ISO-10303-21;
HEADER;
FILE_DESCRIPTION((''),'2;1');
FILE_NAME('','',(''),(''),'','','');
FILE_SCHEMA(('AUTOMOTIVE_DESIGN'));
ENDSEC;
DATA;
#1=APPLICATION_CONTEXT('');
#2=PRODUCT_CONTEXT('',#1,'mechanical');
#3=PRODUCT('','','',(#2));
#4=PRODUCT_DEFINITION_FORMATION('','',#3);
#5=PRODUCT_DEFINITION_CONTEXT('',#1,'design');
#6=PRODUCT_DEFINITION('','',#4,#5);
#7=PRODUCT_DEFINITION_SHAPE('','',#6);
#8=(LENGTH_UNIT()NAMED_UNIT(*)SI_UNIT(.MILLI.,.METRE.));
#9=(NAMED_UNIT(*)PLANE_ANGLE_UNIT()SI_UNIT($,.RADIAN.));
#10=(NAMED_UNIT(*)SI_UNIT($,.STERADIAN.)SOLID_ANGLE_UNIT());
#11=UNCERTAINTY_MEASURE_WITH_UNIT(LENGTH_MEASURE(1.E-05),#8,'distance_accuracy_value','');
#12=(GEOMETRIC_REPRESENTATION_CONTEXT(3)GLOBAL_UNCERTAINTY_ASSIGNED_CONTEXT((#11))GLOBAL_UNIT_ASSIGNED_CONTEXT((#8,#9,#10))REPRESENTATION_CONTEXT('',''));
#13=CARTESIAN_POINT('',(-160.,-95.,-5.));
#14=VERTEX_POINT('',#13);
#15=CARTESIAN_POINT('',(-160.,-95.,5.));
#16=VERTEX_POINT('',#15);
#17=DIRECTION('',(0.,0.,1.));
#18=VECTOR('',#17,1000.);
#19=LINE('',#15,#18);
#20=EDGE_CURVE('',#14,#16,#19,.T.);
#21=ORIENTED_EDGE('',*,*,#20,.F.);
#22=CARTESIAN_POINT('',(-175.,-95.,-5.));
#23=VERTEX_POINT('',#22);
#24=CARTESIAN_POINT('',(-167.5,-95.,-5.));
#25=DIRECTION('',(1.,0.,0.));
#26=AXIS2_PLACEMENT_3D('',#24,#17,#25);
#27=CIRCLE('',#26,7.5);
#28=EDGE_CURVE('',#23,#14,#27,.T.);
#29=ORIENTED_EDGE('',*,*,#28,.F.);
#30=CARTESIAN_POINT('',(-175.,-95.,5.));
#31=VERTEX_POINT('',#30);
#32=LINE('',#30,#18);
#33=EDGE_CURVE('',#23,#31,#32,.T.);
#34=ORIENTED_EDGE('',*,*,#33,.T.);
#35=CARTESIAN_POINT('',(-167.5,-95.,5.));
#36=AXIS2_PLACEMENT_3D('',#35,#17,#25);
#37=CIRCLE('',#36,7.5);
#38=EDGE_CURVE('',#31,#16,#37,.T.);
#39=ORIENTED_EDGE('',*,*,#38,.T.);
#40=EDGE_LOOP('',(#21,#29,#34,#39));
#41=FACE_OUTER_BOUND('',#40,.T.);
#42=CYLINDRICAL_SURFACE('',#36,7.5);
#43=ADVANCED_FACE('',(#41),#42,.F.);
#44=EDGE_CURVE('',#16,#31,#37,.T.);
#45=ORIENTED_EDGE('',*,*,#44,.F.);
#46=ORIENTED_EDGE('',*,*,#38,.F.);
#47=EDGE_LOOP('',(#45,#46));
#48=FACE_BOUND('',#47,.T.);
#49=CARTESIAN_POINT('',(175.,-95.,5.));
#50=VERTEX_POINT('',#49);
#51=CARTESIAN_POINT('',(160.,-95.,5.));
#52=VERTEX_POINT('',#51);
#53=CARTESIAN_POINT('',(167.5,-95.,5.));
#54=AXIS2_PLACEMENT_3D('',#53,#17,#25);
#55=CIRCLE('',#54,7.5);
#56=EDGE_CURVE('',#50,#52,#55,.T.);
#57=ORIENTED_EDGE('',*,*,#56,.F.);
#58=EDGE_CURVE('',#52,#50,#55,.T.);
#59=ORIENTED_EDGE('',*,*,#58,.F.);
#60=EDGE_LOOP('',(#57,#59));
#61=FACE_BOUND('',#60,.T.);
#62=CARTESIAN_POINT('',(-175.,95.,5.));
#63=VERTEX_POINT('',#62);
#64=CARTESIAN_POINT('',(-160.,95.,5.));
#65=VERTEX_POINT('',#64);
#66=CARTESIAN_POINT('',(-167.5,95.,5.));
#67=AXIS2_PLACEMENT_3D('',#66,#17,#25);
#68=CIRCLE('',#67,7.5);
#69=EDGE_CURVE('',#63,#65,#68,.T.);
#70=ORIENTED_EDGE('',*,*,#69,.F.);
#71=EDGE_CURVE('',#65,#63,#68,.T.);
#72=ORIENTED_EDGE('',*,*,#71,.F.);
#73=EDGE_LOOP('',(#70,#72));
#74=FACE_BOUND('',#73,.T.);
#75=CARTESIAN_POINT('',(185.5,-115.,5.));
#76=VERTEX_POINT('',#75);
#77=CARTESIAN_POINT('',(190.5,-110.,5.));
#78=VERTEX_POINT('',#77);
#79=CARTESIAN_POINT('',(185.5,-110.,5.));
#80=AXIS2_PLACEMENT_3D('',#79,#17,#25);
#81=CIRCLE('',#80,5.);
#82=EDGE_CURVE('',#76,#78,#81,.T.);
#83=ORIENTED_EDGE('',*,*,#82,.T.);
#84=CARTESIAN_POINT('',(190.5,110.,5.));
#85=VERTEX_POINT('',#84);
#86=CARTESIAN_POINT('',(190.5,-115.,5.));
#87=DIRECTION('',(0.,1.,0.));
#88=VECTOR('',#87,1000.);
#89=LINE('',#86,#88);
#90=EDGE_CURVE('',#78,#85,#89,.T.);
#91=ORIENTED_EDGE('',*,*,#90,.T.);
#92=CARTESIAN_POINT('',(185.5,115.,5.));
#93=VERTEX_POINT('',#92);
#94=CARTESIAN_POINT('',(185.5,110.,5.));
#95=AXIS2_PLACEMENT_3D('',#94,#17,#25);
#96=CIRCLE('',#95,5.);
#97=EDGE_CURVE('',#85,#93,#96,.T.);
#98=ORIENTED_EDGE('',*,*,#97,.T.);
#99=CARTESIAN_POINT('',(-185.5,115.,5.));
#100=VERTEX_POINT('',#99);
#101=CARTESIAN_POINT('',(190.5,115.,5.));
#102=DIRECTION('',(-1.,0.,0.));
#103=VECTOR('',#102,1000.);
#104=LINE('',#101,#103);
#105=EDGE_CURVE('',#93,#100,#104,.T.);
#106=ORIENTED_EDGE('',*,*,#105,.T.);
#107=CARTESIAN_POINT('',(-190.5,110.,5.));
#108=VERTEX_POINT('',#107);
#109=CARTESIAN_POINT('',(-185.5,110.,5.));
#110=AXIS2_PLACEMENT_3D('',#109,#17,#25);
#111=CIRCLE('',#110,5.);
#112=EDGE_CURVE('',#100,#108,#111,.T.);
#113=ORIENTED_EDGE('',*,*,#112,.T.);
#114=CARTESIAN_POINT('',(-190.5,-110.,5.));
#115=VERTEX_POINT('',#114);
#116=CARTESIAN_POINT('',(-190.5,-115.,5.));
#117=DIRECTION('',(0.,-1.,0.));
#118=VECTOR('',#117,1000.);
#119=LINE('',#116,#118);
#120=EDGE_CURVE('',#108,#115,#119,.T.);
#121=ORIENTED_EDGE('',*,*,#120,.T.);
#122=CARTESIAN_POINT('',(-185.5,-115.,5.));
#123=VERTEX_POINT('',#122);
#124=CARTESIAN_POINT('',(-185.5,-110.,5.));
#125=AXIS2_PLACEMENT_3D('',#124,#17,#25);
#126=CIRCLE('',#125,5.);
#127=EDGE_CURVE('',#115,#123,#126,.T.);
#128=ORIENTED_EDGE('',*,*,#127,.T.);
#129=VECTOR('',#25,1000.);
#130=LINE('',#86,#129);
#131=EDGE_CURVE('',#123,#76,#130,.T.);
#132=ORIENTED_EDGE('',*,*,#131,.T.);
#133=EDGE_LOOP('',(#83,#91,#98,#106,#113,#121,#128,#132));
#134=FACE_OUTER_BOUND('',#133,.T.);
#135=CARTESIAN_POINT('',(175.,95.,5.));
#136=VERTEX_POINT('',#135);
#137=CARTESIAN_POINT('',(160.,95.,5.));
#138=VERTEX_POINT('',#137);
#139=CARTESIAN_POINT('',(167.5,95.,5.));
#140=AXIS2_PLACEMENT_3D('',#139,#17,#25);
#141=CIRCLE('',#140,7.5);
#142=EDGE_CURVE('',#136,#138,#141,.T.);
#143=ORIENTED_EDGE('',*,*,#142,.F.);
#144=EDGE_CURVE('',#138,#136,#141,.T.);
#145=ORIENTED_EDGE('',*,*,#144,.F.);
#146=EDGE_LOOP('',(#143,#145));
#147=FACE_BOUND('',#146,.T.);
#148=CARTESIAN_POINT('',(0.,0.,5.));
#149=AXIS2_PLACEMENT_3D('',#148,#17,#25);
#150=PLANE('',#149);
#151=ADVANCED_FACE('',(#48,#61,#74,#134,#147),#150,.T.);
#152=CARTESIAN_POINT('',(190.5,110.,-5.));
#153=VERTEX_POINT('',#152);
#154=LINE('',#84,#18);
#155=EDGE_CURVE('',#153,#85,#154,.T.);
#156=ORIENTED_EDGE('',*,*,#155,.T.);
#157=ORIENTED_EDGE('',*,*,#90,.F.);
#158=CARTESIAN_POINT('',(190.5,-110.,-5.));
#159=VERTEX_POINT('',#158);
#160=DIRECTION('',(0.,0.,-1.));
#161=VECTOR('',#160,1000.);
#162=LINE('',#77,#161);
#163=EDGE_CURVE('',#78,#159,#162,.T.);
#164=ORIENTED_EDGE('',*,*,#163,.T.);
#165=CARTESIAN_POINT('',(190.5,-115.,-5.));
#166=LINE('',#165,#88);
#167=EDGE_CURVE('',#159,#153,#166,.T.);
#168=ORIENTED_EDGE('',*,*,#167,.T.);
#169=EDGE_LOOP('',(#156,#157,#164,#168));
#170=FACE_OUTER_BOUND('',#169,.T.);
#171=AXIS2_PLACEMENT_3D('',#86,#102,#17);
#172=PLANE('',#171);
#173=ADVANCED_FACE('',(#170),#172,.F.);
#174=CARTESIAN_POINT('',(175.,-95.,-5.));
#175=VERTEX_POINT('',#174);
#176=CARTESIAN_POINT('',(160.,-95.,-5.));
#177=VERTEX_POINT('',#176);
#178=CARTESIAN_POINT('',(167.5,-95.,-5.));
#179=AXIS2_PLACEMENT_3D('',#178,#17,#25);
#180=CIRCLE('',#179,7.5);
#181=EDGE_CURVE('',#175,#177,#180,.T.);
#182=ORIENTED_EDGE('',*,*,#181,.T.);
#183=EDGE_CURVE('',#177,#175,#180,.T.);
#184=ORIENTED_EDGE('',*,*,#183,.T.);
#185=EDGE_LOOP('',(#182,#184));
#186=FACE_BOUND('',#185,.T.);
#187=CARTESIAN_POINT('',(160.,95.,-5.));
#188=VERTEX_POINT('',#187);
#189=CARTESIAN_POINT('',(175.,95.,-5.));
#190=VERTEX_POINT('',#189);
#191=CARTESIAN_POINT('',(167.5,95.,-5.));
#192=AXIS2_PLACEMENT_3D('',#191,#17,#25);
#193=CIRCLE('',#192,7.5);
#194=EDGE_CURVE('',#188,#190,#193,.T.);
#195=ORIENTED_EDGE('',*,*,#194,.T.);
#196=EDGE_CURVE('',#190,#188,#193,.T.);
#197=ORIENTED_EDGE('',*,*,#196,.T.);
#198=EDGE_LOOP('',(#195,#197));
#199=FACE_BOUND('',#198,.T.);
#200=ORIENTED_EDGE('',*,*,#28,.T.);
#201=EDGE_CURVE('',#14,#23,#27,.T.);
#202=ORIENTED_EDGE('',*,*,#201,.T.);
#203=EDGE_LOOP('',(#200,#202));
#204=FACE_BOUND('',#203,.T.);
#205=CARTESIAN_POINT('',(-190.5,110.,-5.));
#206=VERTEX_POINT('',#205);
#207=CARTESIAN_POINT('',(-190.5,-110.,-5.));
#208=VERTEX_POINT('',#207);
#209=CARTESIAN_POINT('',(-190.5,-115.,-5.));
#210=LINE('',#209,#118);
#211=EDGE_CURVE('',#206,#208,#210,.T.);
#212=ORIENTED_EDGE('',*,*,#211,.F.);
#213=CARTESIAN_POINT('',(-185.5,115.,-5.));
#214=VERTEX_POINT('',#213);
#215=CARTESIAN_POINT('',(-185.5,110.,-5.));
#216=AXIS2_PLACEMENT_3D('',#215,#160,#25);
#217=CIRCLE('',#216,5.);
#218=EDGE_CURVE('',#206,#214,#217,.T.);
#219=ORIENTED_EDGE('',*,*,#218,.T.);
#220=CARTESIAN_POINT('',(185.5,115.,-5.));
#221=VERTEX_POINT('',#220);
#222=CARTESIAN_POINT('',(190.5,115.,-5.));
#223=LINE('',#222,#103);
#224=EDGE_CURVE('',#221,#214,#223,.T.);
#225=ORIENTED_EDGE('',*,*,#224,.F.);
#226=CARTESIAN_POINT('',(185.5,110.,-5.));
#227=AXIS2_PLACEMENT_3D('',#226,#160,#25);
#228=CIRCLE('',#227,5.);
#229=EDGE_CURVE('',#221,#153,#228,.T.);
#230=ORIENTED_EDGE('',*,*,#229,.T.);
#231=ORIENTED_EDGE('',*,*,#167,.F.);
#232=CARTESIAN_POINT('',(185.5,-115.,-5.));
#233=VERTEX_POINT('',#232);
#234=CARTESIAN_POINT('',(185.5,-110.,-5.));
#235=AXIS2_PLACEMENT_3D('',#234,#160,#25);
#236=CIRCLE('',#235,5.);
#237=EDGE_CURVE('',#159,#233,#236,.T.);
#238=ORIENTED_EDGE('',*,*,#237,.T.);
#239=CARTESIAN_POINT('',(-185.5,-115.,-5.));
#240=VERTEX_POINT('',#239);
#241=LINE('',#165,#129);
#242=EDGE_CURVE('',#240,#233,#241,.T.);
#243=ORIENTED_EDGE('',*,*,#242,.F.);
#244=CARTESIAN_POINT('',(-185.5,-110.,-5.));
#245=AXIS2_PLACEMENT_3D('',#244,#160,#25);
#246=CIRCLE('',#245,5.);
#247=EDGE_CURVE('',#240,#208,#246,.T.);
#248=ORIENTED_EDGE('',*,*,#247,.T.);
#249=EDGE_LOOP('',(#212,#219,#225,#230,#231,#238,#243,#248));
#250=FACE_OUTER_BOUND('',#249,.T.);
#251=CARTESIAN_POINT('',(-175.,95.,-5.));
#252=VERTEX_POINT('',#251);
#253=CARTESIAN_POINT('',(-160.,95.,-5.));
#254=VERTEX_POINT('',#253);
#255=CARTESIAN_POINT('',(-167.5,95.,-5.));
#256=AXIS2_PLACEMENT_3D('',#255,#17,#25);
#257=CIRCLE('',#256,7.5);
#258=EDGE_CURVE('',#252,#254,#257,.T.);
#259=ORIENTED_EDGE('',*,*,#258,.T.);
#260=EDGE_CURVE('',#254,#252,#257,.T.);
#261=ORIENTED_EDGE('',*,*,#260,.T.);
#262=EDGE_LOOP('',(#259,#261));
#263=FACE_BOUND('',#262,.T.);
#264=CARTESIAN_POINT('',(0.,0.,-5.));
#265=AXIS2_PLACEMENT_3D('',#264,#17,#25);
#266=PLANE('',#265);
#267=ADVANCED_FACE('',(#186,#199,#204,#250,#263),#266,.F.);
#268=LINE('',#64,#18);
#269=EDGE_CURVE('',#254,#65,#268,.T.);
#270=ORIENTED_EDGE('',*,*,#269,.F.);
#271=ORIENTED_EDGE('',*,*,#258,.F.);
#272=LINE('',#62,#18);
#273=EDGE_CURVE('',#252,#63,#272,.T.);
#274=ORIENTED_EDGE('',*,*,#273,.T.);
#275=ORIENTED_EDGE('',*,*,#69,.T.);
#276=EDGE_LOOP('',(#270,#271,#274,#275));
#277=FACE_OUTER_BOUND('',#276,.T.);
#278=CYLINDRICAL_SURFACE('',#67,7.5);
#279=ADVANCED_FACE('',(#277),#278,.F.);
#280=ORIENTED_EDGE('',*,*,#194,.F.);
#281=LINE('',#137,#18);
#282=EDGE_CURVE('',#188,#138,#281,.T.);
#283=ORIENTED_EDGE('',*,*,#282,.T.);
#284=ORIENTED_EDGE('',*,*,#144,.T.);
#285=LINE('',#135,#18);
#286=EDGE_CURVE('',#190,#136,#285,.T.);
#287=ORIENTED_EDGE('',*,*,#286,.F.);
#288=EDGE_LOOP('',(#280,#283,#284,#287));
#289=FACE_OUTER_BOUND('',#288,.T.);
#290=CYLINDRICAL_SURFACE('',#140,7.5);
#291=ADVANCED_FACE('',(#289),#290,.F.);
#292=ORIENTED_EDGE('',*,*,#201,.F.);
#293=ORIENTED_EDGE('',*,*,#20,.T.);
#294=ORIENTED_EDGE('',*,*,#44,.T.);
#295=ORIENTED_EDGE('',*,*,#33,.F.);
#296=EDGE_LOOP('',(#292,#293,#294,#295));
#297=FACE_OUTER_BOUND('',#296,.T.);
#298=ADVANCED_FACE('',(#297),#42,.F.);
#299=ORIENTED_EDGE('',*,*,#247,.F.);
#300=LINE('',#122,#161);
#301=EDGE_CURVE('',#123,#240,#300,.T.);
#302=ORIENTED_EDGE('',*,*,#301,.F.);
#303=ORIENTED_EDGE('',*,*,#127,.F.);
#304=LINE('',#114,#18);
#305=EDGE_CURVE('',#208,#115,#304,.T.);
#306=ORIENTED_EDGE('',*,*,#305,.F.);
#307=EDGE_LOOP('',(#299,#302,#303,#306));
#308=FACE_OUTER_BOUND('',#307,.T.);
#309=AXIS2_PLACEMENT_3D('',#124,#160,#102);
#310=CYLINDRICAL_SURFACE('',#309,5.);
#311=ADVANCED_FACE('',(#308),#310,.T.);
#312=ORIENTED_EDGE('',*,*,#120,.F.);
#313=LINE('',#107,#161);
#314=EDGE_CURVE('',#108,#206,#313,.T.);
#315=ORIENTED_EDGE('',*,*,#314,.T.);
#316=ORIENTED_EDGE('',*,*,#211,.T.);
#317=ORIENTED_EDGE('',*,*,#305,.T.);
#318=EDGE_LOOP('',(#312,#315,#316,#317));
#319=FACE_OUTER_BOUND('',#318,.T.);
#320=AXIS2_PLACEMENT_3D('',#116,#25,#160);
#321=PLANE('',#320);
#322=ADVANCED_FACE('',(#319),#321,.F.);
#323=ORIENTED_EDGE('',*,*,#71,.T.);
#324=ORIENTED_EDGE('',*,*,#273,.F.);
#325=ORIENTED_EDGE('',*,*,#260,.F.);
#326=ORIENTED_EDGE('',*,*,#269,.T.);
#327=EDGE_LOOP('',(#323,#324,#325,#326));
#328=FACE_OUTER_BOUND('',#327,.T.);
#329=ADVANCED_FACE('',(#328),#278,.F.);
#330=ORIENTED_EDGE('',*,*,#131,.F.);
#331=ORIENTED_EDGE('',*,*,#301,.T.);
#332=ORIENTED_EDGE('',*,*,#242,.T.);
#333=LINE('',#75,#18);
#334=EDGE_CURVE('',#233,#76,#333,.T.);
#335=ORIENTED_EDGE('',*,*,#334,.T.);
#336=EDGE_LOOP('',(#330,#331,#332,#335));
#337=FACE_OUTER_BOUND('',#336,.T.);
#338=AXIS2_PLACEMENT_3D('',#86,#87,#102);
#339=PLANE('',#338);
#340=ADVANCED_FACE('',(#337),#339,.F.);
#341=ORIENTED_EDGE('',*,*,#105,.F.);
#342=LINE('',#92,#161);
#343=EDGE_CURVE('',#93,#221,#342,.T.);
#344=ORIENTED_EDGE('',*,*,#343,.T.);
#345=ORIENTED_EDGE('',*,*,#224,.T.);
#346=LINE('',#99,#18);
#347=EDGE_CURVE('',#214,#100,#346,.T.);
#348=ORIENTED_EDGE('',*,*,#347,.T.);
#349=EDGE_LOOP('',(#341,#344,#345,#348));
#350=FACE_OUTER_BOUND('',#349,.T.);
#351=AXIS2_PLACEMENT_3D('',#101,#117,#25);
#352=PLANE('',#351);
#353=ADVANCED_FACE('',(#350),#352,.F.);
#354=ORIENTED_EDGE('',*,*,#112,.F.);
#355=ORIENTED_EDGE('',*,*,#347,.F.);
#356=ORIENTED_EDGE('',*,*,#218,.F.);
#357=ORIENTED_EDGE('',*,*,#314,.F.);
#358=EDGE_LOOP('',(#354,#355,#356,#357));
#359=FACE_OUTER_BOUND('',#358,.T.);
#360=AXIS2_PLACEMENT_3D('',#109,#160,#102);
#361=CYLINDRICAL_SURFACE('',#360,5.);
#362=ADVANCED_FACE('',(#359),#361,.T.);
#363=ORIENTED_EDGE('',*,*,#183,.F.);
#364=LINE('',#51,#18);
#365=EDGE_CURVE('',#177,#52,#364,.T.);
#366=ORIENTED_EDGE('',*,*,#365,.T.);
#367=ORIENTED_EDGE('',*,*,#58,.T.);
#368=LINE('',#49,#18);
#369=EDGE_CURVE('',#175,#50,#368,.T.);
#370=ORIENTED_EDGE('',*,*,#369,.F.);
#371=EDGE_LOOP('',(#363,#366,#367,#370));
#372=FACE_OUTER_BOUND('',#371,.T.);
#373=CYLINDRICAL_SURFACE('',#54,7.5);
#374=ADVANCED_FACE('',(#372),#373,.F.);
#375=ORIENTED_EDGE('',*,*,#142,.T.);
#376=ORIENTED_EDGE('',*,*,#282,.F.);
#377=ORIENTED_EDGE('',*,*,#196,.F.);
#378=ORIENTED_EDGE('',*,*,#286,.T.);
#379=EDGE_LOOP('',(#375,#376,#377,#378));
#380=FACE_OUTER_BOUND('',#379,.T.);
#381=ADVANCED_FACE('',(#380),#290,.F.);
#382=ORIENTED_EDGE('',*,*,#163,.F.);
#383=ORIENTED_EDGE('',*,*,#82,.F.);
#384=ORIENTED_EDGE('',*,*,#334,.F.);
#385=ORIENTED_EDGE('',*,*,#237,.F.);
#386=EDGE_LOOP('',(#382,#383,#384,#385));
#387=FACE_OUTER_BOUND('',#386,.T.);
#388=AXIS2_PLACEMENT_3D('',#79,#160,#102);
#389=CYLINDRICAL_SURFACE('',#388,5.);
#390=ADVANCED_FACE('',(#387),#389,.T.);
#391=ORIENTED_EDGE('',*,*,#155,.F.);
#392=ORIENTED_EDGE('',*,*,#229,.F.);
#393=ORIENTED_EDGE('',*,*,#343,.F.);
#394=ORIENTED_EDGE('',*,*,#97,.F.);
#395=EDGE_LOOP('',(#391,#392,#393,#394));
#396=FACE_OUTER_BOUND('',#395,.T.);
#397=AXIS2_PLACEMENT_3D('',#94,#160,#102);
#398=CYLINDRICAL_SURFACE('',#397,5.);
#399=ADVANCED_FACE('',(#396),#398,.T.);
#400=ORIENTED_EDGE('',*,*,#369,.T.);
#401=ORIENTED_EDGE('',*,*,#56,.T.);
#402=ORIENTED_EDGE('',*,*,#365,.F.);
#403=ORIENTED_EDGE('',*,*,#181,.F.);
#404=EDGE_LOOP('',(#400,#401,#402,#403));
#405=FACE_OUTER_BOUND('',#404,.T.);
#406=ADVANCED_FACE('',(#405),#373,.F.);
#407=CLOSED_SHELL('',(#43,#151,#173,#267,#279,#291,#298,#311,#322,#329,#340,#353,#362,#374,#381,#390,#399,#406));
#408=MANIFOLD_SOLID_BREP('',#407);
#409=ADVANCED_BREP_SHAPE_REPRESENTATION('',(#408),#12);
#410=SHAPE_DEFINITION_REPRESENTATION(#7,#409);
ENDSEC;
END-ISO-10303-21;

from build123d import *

# Parameters (mm, degrees)
SKETCH1_W           = 381
SKETCH1_H           = 230
BOSS_EXTRUDE1_DEPTH = 5
F_15_HOLE1_D        = 15
FILLET2_R           = 5


with BuildPart() as part:
    # Sketch1 → Boss-Extrude1 (new, symmetric)
    with BuildSketch(Plane.XY):
        Rectangle(SKETCH1_W, SKETCH1_H)
    extrude(amount=BOSS_EXTRUDE1_DEPTH, both=True)

    # Ø15 Hole1 (through all)
    with Locations(Plane.XY.offset(5)):
        with Locations((-167.5, 95), (167.5, 95), (167.5, -95), (-167.5, -95)):
            Hole(F_15_HOLE1_D / 2)

    # Fillet2
    fillet2_edges = [part.edges().sort_by_distance(p)[0] for p in [
        (-190.5, 115, 0),
        (190.5, 115, 0),
        (190.5, -115, 0),
        (-190.5, -115, 0),
    ]]
    fillet(fillet2_edges, radius=FILLET2_R)


solid = part.part
